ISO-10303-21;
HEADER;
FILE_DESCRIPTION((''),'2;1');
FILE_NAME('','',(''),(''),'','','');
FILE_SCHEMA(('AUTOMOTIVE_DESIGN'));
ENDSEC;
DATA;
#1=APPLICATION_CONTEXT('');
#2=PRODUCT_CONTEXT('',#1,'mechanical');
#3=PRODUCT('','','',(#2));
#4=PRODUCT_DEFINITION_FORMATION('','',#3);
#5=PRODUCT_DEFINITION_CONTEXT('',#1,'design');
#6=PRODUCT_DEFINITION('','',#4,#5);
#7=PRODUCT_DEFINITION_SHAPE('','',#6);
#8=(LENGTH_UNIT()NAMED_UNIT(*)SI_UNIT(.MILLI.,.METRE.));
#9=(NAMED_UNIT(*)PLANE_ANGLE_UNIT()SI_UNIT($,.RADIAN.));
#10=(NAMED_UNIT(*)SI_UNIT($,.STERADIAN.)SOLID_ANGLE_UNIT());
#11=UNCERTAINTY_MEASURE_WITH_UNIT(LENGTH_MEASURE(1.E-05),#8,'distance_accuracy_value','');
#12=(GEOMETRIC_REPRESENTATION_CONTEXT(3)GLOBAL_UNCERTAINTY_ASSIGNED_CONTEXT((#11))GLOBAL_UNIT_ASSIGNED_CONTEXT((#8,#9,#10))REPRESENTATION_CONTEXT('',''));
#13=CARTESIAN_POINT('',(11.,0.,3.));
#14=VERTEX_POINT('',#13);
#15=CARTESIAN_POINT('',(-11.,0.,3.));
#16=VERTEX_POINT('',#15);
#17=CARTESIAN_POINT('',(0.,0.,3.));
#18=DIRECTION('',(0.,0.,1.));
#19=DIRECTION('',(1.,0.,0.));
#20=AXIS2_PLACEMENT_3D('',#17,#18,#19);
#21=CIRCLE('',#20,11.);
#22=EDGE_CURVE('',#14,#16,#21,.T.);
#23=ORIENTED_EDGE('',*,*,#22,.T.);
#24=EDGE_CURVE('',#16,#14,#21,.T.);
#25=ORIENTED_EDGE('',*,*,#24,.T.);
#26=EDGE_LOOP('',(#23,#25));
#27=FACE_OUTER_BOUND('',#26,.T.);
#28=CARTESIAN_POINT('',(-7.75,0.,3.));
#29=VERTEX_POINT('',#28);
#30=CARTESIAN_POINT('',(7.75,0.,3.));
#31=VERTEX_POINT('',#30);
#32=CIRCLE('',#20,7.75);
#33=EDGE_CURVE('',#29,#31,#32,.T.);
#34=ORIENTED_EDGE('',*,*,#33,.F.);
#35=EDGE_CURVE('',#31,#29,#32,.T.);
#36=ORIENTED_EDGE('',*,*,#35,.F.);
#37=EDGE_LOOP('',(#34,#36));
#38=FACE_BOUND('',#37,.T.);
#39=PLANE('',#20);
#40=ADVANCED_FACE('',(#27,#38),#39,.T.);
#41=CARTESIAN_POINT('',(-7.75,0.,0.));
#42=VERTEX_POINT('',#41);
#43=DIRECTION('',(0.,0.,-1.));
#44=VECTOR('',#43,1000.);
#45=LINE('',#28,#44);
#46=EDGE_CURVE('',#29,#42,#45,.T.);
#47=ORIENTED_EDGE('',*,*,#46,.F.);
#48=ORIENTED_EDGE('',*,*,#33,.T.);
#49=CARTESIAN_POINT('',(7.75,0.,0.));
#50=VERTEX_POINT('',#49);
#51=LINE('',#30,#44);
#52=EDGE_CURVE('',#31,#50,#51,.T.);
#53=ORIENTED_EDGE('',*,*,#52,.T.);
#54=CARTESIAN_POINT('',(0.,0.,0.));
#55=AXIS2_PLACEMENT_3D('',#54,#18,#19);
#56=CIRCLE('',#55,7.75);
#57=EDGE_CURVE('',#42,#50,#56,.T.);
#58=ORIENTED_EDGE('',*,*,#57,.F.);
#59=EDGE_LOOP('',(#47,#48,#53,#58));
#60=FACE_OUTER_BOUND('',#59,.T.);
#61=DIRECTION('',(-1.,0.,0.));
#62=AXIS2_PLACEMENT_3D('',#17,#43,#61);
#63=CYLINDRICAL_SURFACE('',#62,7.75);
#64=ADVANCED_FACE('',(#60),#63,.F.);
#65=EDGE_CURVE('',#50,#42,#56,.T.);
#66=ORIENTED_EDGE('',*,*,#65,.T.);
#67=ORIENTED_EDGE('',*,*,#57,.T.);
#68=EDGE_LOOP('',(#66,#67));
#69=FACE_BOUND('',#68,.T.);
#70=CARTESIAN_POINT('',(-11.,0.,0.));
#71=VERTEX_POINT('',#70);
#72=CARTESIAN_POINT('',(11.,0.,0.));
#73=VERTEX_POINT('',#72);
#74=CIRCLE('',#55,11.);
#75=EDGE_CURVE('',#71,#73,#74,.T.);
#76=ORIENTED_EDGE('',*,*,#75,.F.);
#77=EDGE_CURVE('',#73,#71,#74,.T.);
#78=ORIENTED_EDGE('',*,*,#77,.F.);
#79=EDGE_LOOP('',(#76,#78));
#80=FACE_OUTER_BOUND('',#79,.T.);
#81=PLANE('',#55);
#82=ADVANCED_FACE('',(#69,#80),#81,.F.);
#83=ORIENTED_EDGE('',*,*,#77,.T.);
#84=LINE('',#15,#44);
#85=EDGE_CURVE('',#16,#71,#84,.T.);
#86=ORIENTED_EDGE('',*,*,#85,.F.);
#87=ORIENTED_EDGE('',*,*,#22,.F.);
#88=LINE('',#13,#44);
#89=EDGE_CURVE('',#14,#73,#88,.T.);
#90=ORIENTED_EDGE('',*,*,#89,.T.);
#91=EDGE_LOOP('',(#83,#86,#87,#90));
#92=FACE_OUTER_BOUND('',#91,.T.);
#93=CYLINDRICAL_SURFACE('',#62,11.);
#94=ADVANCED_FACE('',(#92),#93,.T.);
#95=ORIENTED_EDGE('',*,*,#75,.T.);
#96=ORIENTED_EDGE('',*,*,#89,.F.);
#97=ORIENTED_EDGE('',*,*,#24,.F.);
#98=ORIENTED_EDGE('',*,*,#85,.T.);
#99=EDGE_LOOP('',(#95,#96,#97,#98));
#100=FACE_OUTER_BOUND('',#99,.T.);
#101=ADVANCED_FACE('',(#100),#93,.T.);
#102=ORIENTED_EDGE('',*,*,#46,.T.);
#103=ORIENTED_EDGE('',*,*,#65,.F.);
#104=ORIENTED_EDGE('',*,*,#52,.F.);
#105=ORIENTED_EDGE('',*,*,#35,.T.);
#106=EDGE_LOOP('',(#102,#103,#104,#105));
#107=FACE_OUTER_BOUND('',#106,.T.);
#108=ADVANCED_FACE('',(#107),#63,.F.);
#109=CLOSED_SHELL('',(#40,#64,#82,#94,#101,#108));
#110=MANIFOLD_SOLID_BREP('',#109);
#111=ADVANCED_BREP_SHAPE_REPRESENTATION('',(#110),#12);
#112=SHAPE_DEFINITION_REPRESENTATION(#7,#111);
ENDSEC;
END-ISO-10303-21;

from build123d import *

# Parameters (mm, degrees)
SKETCH_1_R      = 11
SKETCH_1_R_2    = 7.75
EXTRUDE_1_DEPTH = 3


with BuildPart() as part:
    # 草图1 → 凸台-拉伸1 (new body)
    with BuildSketch(Plane.XY):
        Circle(SKETCH_1_R)
        Circle(SKETCH_1_R_2, mode=Mode.SUBTRACT)
    extrude(amount=EXTRUDE_1_DEPTH)


solid = part.part
